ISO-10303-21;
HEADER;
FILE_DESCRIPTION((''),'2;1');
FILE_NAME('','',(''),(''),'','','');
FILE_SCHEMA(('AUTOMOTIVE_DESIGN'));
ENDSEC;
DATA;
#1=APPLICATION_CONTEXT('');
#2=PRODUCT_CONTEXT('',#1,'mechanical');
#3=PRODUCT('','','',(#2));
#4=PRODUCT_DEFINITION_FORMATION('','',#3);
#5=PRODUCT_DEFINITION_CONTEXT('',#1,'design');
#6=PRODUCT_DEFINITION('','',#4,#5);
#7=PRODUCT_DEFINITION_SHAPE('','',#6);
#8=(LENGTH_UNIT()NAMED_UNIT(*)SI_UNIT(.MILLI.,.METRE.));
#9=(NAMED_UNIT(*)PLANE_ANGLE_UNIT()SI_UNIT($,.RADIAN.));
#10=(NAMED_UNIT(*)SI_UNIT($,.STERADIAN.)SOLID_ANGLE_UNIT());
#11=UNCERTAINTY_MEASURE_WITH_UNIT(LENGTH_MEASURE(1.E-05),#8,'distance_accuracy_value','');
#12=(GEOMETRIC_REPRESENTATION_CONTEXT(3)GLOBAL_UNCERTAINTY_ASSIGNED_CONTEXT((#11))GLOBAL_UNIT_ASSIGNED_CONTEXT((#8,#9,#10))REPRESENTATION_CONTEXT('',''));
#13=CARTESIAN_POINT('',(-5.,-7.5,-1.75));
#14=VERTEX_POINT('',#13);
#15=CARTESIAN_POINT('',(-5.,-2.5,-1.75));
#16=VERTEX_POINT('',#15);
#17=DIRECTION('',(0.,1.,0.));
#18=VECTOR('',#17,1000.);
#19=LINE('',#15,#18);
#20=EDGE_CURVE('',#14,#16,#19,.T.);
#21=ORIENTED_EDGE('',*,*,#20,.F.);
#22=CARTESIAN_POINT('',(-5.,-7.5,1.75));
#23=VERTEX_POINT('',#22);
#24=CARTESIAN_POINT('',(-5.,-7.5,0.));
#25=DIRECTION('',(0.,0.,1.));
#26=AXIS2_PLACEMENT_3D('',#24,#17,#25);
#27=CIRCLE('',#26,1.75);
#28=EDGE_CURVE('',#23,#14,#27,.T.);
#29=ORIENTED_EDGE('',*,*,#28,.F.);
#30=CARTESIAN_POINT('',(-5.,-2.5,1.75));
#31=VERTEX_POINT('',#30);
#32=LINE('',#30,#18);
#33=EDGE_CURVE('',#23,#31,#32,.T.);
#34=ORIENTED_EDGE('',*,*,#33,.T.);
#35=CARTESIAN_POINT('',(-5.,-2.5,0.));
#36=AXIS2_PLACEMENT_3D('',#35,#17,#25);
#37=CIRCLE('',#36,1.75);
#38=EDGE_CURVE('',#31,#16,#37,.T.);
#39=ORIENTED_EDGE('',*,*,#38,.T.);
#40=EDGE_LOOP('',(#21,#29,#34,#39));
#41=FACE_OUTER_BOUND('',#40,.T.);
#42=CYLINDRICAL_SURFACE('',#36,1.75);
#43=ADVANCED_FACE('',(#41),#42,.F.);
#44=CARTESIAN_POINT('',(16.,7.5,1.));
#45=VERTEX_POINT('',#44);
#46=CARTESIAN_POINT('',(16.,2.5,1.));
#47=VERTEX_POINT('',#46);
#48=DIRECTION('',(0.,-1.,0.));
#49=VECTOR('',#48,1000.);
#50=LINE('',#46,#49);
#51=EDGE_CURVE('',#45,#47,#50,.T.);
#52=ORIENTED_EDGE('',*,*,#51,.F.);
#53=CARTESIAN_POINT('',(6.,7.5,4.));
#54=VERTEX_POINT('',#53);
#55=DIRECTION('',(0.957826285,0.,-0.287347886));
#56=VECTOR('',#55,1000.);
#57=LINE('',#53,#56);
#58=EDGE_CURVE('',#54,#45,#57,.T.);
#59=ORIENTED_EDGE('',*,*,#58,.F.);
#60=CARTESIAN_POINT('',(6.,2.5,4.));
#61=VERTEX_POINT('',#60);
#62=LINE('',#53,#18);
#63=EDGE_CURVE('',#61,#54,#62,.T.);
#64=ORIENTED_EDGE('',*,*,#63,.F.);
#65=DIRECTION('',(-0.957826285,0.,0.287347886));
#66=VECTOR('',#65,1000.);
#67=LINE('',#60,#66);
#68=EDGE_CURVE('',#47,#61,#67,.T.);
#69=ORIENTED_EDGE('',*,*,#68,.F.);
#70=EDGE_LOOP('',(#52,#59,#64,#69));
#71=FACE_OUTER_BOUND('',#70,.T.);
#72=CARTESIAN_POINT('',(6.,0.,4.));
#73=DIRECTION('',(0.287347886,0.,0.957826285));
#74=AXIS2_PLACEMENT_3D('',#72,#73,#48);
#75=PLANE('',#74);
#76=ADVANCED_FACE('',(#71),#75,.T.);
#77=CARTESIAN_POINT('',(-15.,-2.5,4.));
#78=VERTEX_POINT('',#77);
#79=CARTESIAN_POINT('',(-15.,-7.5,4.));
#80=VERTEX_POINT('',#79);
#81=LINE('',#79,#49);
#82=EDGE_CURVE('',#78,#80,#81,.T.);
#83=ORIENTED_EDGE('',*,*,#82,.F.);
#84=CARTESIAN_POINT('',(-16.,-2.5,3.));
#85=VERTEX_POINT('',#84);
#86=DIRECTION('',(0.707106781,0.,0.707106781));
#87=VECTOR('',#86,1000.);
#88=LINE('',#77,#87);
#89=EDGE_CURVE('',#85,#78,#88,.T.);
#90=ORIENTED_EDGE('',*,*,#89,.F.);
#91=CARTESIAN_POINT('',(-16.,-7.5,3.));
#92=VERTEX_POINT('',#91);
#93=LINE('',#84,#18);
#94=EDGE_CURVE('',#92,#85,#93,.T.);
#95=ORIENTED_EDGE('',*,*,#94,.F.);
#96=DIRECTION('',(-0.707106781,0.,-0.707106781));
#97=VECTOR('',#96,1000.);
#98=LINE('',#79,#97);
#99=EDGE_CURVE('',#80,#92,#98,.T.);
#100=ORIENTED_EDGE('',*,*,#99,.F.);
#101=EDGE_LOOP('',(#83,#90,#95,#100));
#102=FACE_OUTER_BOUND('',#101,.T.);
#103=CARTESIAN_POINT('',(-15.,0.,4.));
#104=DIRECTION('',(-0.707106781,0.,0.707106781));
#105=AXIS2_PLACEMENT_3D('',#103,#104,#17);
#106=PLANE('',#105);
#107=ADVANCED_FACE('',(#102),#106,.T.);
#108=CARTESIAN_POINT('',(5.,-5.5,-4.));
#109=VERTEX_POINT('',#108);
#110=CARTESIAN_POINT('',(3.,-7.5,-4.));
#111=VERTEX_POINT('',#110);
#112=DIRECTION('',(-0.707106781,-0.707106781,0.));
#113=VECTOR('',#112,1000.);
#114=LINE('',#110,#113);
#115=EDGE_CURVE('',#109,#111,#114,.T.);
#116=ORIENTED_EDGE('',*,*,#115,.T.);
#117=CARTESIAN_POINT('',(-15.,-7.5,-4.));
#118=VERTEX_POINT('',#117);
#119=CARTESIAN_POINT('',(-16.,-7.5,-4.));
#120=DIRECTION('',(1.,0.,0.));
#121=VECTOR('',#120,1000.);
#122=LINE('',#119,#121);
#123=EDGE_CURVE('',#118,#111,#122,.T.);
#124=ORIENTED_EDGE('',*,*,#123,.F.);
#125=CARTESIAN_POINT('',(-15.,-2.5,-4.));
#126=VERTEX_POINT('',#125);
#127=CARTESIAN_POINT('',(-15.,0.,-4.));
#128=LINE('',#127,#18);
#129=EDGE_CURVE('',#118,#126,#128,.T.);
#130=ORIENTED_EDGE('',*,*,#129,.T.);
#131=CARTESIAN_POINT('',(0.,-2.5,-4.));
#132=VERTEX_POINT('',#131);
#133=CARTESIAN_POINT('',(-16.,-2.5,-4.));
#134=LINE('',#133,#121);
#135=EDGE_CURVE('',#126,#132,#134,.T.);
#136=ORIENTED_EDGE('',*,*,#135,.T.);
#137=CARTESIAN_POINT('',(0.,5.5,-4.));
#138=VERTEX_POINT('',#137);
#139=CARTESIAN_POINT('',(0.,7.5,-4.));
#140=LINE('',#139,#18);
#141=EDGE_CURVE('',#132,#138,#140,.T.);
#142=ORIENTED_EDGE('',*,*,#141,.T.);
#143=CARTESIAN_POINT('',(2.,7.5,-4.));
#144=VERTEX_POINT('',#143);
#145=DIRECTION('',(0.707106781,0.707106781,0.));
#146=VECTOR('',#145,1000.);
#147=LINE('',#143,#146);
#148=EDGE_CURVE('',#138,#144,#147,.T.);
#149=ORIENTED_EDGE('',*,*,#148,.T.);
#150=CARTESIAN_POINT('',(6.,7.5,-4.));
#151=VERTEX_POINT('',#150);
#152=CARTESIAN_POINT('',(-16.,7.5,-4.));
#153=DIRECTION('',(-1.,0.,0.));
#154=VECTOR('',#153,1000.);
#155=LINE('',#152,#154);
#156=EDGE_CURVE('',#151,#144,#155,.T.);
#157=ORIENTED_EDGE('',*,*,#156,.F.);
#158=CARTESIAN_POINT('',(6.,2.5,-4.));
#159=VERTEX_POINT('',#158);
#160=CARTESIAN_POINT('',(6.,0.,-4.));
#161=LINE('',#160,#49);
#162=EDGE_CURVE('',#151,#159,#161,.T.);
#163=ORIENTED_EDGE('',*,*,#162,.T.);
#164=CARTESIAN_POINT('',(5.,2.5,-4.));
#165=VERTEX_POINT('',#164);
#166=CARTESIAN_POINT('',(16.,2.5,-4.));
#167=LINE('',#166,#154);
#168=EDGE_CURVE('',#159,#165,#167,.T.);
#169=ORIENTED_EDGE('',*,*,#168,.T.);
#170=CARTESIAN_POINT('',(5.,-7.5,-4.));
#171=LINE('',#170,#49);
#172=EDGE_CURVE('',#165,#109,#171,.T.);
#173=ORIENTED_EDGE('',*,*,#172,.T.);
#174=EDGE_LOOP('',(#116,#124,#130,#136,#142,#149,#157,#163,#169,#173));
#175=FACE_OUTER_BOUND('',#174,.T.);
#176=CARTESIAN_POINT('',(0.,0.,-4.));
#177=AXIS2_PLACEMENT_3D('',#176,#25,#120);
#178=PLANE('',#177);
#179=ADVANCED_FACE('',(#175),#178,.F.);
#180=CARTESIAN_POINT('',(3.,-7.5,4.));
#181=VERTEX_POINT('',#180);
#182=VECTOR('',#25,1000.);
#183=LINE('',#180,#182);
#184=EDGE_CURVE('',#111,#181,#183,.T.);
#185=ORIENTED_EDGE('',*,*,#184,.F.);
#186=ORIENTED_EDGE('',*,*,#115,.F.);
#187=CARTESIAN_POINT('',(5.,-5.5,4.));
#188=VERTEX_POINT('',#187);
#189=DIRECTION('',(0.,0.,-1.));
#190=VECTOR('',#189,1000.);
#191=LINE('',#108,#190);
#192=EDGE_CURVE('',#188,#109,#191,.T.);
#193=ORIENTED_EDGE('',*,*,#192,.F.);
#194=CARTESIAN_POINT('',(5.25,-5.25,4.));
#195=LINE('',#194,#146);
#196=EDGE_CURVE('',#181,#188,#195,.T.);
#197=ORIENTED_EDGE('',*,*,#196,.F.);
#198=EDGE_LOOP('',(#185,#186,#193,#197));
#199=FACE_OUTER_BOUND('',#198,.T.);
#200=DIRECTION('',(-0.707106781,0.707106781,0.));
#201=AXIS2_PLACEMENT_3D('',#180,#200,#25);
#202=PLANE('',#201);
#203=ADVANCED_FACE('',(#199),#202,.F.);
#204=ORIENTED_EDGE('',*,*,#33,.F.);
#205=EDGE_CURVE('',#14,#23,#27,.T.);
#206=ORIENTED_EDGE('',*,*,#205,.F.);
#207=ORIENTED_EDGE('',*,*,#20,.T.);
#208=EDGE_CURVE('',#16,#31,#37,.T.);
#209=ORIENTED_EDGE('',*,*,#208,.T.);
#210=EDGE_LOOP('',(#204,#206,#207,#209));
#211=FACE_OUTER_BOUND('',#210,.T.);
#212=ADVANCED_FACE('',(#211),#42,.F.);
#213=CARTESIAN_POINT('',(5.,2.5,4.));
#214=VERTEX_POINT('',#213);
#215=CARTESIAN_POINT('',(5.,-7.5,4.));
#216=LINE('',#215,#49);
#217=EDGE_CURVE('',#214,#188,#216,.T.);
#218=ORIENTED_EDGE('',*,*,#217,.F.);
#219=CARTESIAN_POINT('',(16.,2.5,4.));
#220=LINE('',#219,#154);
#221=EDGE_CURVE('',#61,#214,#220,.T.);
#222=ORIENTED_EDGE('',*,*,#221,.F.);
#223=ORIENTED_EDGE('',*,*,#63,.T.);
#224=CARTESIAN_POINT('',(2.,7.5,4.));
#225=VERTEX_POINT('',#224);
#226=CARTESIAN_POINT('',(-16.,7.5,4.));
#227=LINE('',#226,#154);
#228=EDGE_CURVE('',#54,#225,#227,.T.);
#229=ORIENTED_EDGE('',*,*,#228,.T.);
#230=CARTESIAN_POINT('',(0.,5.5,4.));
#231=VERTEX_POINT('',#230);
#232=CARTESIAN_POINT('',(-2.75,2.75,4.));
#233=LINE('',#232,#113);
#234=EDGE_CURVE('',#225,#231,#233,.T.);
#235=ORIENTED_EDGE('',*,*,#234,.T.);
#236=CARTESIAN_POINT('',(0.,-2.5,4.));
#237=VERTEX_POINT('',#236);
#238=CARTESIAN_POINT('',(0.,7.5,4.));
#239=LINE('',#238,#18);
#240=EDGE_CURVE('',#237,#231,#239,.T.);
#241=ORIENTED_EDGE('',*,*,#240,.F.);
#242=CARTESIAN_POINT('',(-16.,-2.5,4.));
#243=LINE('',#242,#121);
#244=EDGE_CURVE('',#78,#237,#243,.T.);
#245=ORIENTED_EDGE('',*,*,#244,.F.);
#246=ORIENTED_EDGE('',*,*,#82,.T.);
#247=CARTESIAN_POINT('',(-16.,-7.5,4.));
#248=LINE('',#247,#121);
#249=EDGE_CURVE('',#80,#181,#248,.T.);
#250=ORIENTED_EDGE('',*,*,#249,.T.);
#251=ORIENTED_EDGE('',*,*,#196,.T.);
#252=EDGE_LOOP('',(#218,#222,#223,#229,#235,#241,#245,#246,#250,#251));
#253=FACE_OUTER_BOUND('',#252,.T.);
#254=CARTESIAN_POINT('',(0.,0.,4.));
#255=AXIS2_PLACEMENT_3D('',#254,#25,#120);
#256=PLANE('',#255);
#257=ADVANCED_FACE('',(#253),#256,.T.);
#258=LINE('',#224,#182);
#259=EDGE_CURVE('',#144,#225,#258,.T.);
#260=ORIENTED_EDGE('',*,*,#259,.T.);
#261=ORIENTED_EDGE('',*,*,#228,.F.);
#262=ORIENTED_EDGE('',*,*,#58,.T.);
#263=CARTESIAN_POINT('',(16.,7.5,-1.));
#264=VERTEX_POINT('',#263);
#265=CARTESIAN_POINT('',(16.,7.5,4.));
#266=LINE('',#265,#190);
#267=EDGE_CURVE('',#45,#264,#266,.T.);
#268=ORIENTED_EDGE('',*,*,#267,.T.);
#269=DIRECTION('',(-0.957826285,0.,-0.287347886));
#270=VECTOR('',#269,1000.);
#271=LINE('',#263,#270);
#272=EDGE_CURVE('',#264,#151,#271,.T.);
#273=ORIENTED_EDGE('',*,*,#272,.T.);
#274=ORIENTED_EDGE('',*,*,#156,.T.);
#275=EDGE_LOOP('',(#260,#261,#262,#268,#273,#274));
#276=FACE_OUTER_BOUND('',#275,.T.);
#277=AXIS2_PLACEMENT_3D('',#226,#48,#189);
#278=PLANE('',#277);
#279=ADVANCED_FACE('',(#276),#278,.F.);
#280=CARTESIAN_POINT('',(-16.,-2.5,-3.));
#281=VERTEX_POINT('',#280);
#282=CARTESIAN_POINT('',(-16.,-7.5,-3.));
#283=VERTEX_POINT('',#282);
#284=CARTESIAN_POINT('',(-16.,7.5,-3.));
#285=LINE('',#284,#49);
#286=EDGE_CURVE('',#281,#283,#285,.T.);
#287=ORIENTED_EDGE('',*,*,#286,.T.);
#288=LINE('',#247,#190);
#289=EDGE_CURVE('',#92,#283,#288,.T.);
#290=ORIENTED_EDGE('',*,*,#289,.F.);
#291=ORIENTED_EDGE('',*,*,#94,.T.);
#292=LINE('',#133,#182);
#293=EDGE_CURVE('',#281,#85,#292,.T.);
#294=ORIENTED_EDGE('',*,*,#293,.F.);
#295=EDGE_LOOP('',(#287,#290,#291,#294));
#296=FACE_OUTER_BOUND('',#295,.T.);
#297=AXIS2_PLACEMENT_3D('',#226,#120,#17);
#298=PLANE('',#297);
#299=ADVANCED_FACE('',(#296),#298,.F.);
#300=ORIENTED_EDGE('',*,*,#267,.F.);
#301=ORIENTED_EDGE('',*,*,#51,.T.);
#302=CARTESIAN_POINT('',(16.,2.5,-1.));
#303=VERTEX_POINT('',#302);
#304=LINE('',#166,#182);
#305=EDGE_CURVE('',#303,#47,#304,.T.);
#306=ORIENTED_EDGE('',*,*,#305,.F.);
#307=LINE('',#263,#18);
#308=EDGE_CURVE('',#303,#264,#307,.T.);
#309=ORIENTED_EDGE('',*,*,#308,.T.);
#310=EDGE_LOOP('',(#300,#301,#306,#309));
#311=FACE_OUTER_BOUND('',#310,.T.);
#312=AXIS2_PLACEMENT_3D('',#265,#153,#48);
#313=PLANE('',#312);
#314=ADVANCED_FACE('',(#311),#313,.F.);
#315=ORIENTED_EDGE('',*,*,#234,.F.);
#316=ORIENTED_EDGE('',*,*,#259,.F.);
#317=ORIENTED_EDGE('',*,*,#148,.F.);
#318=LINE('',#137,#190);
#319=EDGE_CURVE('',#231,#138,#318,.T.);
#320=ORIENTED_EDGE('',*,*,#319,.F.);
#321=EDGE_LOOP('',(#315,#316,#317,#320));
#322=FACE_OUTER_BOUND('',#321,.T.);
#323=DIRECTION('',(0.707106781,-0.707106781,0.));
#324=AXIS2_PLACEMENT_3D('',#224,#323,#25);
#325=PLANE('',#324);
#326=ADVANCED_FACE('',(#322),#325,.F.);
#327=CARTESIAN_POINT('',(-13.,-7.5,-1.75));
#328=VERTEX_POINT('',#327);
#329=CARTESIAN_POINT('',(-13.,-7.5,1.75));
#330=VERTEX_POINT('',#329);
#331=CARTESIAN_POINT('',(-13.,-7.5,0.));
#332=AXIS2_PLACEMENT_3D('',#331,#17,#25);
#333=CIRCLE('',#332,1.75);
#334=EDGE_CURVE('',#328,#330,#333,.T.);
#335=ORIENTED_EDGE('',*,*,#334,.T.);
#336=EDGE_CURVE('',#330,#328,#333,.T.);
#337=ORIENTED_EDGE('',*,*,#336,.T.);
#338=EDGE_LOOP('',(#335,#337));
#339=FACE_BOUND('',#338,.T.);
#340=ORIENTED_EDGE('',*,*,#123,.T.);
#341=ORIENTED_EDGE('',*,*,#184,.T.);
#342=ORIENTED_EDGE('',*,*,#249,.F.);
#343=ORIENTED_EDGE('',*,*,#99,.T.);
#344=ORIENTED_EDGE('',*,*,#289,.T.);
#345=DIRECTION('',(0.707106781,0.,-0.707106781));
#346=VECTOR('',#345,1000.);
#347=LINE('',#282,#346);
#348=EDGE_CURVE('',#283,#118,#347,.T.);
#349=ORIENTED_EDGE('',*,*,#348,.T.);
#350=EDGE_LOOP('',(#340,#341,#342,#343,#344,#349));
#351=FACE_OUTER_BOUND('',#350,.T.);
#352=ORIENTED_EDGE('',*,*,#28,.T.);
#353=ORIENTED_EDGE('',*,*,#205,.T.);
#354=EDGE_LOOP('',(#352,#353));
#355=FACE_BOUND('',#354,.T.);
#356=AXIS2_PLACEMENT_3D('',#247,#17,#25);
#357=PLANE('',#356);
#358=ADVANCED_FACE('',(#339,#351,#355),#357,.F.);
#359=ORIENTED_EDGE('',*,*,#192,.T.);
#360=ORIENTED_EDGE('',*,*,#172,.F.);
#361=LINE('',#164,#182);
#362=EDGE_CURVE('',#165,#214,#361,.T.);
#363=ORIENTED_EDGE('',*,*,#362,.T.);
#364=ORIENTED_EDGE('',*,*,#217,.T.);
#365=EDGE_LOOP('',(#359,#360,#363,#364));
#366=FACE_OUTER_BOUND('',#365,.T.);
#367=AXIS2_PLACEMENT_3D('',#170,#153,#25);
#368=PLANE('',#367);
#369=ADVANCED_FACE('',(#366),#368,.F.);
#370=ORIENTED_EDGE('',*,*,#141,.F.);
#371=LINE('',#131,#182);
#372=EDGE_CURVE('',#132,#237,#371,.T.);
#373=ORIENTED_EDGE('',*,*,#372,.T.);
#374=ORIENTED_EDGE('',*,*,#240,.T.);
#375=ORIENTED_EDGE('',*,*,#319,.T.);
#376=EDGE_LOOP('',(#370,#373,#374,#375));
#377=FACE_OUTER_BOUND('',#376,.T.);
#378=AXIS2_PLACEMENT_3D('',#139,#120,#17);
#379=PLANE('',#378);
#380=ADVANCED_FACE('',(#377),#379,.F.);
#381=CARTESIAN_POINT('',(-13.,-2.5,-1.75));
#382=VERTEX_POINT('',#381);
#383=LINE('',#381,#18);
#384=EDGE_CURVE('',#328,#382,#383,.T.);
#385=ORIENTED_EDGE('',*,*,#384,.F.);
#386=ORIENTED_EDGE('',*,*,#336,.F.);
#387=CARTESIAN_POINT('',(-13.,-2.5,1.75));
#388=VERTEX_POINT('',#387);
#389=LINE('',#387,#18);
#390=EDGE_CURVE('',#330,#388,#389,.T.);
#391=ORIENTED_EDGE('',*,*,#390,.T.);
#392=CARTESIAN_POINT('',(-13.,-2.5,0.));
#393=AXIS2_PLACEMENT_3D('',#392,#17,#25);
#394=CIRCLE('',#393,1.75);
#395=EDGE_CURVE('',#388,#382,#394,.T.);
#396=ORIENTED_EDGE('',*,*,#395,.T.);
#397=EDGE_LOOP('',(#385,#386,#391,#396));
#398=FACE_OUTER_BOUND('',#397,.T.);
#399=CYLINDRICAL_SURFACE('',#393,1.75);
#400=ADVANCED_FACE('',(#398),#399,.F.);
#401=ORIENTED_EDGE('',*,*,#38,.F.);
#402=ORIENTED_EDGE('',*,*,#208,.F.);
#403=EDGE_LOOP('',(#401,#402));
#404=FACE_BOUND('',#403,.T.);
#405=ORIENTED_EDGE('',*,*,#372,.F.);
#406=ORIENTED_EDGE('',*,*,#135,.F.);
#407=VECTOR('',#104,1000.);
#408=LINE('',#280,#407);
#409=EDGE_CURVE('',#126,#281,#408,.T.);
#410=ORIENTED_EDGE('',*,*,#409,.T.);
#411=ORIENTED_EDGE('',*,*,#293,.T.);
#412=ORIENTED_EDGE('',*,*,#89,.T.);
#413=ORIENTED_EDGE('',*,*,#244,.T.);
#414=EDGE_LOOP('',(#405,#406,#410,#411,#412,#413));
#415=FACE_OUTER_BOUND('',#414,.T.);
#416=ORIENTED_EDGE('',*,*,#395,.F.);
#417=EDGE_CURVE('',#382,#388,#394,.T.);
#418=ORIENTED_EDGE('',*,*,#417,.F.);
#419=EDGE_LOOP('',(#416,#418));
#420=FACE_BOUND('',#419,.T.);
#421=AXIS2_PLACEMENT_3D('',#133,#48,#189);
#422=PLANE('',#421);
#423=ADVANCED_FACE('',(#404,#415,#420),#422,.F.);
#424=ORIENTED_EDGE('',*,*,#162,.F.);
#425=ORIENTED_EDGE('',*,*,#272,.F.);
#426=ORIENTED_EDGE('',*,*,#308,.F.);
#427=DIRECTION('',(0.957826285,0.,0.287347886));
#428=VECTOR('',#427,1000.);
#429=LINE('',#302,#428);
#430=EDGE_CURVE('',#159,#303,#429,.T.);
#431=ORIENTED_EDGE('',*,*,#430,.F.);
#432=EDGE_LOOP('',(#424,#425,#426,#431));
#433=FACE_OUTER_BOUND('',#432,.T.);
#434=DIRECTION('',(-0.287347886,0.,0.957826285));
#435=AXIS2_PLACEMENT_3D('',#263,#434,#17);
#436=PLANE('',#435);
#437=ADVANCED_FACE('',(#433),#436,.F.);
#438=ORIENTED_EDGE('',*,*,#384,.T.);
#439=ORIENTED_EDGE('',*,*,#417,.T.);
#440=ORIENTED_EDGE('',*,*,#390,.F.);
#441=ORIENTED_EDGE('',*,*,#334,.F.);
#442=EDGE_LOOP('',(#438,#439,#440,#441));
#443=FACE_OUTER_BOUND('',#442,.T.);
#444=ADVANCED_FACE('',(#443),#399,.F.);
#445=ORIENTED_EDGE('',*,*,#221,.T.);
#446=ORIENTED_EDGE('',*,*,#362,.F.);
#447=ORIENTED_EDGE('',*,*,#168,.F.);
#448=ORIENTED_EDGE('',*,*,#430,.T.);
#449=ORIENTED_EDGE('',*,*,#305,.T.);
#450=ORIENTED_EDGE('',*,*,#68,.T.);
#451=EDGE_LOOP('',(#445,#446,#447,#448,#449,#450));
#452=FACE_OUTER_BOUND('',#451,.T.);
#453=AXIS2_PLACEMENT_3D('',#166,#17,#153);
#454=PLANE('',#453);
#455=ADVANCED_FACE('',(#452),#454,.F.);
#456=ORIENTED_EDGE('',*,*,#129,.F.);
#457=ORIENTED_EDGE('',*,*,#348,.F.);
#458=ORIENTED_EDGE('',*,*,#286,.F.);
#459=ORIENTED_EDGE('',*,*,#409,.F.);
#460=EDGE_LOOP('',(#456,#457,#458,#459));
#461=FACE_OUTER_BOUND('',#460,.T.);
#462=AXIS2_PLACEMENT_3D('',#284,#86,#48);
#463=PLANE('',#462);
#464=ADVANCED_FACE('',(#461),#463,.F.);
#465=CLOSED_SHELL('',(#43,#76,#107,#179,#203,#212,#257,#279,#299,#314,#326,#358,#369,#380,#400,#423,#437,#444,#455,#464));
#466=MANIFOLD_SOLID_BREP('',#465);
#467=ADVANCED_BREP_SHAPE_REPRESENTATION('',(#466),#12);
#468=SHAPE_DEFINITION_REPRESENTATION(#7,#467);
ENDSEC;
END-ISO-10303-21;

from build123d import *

# Parameters (mm, degrees)
SKETCH1_W                  = 32
SKETCH1_H                  = 15
BOSS_EXTRUDE1_DEPTH        = 4
SKETCH2_W                  = 16
SKETCH2_H                  = 10
SKETCH2_W_2                = 11
CUT_EXTRUDE1_DEPTH         = 20.397164741
CHAMFER1_SIZE              = 1
CHAMFER2_SIZE              = 2
F_3_5_3_5_DIAMETER_HOLE1_D = 3.5
CHAMFER3_SIZE              = 3
CHAMFER3_SIZE2             = 10
CHAMFER4_SIZE              = 10
CHAMFER4_SIZE2             = 3


with BuildPart() as part:
    # Sketch1 → Boss-Extrude1 (new, symmetric)
    with BuildSketch(Plane.XY):
        Rectangle(SKETCH1_W, SKETCH1_H)
    extrude(amount=BOSS_EXTRUDE1_DEPTH, both=True)

    # Sketch2 → Cut-Extrude1 (cut, through all)
    with BuildSketch(Plane.XY.offset(4)):
        with Locations((-8, 2.5)):
            Rectangle(SKETCH2_W, SKETCH2_H)
        with Locations((10.5, -2.5)):
            Rectangle(SKETCH2_W_2, SKETCH2_H)
    extrude(amount=-CUT_EXTRUDE1_DEPTH, mode=Mode.SUBTRACT)

    # Chamfer1
    chamfer1_edges = [part.edges().sort_by_distance(p)[0] for p in [
        (-16, -5, -4),
        (-16, -5, 4),
    ]]
    chamfer(chamfer1_edges, length=CHAMFER1_SIZE)

    # Chamfer2
    chamfer2_edges = [part.edges().sort_by_distance(p)[0] for p in [
        (0, 7.5, 0),
        (5, -7.5, 0),
    ]]
    chamfer(chamfer2_edges, length=CHAMFER2_SIZE)

    # Ø3.5 (3.5) Diameter Hole1 (through all)
    with Locations(Plane(origin=(0, -2.5, 0), x_dir=(1, 0, 0), z_dir=(0, 1, 0))):
        with Locations((-13, 0), (-5, 0)):
            Hole(F_3_5_3_5_DIAMETER_HOLE1_D / 2)

    # Chamfer3
    chamfer3_edges = [part.edges().sort_by_distance(p)[0] for p in [
        (16, 5, 4),
    ]]
    chamfer3_side = [part.faces().sort_by_distance(p)[0] for p in [
        (16, 5, 0),
    ]]
    chamfer(chamfer3_edges, length=CHAMFER3_SIZE, length2=CHAMFER3_SIZE2, reference=chamfer3_side[0])

    # Chamfer4
    chamfer4_edges = [part.edges().sort_by_distance(p)[0] for p in [
        (16, 5, -4),
    ]]
    chamfer4_side = [part.faces().sort_by_distance(p)[0] for p in [
        (0.957711443, -0.497512438, -4),
    ]]
    chamfer(chamfer4_edges, length=CHAMFER4_SIZE, length2=CHAMFER4_SIZE2, reference=chamfer4_side[0])


solid = part.part
